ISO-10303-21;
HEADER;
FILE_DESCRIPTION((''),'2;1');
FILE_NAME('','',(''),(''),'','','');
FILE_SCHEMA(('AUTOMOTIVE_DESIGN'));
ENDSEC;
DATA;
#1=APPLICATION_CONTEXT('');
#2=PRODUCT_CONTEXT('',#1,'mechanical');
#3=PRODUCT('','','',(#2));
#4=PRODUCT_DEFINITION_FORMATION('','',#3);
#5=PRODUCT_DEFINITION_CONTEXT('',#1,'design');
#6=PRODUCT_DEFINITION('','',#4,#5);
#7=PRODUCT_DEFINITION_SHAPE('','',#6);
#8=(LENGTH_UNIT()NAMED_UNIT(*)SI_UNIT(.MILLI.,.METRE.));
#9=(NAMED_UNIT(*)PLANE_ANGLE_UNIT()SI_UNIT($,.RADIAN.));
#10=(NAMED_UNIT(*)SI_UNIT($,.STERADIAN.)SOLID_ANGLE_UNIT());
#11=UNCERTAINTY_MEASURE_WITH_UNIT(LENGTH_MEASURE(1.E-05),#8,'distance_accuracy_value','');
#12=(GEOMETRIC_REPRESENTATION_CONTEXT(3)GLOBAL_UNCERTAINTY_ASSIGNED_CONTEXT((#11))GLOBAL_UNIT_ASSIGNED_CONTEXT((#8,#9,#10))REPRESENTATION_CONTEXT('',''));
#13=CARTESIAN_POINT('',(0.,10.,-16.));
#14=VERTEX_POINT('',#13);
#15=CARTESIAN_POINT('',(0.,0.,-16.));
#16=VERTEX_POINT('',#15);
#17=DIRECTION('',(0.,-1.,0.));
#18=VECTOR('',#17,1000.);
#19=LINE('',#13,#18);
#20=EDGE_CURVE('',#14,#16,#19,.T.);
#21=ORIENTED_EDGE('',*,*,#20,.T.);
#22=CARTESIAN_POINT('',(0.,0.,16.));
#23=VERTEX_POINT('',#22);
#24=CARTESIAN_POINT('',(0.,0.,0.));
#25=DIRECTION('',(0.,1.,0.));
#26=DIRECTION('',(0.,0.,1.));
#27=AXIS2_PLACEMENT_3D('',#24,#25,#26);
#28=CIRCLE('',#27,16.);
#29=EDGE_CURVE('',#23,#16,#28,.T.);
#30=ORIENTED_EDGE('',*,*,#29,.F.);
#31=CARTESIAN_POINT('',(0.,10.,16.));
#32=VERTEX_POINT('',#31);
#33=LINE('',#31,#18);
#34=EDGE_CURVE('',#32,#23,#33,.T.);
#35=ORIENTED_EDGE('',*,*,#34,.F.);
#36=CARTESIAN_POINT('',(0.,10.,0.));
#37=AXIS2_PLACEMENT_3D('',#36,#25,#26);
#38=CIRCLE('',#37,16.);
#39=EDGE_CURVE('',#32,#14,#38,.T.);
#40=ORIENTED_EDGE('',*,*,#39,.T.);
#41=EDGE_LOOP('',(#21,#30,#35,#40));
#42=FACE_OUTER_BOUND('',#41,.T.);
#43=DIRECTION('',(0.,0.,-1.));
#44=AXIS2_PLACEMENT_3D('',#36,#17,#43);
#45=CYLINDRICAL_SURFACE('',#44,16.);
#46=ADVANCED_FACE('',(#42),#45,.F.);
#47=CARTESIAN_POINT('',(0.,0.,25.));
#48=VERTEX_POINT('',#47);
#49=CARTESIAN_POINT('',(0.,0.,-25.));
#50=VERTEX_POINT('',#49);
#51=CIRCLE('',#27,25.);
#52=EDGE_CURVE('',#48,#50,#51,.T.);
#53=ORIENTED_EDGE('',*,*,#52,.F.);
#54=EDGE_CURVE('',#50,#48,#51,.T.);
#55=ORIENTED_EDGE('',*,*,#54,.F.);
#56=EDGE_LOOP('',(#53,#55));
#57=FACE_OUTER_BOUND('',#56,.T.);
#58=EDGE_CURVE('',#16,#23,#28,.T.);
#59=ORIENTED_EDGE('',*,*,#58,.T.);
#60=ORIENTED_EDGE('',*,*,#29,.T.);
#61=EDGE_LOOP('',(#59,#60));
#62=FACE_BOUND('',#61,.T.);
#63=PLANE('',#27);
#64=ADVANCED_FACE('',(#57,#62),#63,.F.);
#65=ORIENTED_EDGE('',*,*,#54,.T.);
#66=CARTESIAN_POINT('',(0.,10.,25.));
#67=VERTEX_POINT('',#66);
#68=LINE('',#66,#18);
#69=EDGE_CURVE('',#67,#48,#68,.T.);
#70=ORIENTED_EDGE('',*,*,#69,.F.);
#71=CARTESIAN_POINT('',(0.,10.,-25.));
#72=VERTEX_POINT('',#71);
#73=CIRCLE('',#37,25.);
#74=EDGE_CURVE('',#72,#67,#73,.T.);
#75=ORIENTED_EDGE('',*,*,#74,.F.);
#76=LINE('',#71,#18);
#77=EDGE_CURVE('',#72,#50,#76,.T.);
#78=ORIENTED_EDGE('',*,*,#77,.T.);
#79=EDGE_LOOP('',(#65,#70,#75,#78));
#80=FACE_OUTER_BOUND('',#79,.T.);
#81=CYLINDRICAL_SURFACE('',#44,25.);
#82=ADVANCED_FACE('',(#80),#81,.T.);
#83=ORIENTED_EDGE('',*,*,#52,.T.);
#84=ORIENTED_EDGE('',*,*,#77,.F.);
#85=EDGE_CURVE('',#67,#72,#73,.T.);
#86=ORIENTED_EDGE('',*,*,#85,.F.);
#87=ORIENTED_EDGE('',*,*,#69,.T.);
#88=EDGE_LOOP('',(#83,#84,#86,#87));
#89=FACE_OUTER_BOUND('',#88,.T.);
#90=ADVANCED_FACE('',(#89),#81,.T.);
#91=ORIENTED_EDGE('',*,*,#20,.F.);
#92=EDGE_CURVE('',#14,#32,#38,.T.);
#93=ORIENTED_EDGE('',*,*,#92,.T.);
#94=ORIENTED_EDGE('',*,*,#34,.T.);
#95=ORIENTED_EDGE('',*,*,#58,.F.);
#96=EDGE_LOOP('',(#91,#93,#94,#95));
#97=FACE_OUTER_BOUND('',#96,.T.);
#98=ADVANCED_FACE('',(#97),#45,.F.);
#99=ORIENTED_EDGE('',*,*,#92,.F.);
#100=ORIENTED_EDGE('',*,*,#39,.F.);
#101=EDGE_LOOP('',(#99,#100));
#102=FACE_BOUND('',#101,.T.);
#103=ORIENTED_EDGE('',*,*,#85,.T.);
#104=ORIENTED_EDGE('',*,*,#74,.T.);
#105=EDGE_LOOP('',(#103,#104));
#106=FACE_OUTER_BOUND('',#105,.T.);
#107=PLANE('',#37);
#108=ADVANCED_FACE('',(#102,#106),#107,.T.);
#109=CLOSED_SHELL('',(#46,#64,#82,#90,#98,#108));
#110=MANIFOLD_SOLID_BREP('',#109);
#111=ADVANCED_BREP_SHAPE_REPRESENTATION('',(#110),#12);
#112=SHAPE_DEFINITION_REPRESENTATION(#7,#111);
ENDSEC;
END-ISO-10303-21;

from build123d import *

# Parameters (mm, degrees)
WASHER_PROFILE_50_32_R   = 25
WASHER_PROFILE_50_32_R_2 = 16
WASHER_BODY_10MM_DEPTH   = 10


with BuildPart() as part:
    # Washer Profile Ø50-Ø32 → Washer Body 10mm (new body)
    with BuildSketch(Plane(origin=(0, 0, 0), x_dir=(1, 0, 0), z_dir=(0, 1, 0))):
        with Locations(Location((0, 0, 0), (0, 0, 270))):
            Circle(WASHER_PROFILE_50_32_R)
        with Locations(Location((0, 0, 0), (0, 0, 270))):
            Circle(WASHER_PROFILE_50_32_R_2, mode=Mode.SUBTRACT)
    extrude(amount=WASHER_BODY_10MM_DEPTH)


solid = part.part
